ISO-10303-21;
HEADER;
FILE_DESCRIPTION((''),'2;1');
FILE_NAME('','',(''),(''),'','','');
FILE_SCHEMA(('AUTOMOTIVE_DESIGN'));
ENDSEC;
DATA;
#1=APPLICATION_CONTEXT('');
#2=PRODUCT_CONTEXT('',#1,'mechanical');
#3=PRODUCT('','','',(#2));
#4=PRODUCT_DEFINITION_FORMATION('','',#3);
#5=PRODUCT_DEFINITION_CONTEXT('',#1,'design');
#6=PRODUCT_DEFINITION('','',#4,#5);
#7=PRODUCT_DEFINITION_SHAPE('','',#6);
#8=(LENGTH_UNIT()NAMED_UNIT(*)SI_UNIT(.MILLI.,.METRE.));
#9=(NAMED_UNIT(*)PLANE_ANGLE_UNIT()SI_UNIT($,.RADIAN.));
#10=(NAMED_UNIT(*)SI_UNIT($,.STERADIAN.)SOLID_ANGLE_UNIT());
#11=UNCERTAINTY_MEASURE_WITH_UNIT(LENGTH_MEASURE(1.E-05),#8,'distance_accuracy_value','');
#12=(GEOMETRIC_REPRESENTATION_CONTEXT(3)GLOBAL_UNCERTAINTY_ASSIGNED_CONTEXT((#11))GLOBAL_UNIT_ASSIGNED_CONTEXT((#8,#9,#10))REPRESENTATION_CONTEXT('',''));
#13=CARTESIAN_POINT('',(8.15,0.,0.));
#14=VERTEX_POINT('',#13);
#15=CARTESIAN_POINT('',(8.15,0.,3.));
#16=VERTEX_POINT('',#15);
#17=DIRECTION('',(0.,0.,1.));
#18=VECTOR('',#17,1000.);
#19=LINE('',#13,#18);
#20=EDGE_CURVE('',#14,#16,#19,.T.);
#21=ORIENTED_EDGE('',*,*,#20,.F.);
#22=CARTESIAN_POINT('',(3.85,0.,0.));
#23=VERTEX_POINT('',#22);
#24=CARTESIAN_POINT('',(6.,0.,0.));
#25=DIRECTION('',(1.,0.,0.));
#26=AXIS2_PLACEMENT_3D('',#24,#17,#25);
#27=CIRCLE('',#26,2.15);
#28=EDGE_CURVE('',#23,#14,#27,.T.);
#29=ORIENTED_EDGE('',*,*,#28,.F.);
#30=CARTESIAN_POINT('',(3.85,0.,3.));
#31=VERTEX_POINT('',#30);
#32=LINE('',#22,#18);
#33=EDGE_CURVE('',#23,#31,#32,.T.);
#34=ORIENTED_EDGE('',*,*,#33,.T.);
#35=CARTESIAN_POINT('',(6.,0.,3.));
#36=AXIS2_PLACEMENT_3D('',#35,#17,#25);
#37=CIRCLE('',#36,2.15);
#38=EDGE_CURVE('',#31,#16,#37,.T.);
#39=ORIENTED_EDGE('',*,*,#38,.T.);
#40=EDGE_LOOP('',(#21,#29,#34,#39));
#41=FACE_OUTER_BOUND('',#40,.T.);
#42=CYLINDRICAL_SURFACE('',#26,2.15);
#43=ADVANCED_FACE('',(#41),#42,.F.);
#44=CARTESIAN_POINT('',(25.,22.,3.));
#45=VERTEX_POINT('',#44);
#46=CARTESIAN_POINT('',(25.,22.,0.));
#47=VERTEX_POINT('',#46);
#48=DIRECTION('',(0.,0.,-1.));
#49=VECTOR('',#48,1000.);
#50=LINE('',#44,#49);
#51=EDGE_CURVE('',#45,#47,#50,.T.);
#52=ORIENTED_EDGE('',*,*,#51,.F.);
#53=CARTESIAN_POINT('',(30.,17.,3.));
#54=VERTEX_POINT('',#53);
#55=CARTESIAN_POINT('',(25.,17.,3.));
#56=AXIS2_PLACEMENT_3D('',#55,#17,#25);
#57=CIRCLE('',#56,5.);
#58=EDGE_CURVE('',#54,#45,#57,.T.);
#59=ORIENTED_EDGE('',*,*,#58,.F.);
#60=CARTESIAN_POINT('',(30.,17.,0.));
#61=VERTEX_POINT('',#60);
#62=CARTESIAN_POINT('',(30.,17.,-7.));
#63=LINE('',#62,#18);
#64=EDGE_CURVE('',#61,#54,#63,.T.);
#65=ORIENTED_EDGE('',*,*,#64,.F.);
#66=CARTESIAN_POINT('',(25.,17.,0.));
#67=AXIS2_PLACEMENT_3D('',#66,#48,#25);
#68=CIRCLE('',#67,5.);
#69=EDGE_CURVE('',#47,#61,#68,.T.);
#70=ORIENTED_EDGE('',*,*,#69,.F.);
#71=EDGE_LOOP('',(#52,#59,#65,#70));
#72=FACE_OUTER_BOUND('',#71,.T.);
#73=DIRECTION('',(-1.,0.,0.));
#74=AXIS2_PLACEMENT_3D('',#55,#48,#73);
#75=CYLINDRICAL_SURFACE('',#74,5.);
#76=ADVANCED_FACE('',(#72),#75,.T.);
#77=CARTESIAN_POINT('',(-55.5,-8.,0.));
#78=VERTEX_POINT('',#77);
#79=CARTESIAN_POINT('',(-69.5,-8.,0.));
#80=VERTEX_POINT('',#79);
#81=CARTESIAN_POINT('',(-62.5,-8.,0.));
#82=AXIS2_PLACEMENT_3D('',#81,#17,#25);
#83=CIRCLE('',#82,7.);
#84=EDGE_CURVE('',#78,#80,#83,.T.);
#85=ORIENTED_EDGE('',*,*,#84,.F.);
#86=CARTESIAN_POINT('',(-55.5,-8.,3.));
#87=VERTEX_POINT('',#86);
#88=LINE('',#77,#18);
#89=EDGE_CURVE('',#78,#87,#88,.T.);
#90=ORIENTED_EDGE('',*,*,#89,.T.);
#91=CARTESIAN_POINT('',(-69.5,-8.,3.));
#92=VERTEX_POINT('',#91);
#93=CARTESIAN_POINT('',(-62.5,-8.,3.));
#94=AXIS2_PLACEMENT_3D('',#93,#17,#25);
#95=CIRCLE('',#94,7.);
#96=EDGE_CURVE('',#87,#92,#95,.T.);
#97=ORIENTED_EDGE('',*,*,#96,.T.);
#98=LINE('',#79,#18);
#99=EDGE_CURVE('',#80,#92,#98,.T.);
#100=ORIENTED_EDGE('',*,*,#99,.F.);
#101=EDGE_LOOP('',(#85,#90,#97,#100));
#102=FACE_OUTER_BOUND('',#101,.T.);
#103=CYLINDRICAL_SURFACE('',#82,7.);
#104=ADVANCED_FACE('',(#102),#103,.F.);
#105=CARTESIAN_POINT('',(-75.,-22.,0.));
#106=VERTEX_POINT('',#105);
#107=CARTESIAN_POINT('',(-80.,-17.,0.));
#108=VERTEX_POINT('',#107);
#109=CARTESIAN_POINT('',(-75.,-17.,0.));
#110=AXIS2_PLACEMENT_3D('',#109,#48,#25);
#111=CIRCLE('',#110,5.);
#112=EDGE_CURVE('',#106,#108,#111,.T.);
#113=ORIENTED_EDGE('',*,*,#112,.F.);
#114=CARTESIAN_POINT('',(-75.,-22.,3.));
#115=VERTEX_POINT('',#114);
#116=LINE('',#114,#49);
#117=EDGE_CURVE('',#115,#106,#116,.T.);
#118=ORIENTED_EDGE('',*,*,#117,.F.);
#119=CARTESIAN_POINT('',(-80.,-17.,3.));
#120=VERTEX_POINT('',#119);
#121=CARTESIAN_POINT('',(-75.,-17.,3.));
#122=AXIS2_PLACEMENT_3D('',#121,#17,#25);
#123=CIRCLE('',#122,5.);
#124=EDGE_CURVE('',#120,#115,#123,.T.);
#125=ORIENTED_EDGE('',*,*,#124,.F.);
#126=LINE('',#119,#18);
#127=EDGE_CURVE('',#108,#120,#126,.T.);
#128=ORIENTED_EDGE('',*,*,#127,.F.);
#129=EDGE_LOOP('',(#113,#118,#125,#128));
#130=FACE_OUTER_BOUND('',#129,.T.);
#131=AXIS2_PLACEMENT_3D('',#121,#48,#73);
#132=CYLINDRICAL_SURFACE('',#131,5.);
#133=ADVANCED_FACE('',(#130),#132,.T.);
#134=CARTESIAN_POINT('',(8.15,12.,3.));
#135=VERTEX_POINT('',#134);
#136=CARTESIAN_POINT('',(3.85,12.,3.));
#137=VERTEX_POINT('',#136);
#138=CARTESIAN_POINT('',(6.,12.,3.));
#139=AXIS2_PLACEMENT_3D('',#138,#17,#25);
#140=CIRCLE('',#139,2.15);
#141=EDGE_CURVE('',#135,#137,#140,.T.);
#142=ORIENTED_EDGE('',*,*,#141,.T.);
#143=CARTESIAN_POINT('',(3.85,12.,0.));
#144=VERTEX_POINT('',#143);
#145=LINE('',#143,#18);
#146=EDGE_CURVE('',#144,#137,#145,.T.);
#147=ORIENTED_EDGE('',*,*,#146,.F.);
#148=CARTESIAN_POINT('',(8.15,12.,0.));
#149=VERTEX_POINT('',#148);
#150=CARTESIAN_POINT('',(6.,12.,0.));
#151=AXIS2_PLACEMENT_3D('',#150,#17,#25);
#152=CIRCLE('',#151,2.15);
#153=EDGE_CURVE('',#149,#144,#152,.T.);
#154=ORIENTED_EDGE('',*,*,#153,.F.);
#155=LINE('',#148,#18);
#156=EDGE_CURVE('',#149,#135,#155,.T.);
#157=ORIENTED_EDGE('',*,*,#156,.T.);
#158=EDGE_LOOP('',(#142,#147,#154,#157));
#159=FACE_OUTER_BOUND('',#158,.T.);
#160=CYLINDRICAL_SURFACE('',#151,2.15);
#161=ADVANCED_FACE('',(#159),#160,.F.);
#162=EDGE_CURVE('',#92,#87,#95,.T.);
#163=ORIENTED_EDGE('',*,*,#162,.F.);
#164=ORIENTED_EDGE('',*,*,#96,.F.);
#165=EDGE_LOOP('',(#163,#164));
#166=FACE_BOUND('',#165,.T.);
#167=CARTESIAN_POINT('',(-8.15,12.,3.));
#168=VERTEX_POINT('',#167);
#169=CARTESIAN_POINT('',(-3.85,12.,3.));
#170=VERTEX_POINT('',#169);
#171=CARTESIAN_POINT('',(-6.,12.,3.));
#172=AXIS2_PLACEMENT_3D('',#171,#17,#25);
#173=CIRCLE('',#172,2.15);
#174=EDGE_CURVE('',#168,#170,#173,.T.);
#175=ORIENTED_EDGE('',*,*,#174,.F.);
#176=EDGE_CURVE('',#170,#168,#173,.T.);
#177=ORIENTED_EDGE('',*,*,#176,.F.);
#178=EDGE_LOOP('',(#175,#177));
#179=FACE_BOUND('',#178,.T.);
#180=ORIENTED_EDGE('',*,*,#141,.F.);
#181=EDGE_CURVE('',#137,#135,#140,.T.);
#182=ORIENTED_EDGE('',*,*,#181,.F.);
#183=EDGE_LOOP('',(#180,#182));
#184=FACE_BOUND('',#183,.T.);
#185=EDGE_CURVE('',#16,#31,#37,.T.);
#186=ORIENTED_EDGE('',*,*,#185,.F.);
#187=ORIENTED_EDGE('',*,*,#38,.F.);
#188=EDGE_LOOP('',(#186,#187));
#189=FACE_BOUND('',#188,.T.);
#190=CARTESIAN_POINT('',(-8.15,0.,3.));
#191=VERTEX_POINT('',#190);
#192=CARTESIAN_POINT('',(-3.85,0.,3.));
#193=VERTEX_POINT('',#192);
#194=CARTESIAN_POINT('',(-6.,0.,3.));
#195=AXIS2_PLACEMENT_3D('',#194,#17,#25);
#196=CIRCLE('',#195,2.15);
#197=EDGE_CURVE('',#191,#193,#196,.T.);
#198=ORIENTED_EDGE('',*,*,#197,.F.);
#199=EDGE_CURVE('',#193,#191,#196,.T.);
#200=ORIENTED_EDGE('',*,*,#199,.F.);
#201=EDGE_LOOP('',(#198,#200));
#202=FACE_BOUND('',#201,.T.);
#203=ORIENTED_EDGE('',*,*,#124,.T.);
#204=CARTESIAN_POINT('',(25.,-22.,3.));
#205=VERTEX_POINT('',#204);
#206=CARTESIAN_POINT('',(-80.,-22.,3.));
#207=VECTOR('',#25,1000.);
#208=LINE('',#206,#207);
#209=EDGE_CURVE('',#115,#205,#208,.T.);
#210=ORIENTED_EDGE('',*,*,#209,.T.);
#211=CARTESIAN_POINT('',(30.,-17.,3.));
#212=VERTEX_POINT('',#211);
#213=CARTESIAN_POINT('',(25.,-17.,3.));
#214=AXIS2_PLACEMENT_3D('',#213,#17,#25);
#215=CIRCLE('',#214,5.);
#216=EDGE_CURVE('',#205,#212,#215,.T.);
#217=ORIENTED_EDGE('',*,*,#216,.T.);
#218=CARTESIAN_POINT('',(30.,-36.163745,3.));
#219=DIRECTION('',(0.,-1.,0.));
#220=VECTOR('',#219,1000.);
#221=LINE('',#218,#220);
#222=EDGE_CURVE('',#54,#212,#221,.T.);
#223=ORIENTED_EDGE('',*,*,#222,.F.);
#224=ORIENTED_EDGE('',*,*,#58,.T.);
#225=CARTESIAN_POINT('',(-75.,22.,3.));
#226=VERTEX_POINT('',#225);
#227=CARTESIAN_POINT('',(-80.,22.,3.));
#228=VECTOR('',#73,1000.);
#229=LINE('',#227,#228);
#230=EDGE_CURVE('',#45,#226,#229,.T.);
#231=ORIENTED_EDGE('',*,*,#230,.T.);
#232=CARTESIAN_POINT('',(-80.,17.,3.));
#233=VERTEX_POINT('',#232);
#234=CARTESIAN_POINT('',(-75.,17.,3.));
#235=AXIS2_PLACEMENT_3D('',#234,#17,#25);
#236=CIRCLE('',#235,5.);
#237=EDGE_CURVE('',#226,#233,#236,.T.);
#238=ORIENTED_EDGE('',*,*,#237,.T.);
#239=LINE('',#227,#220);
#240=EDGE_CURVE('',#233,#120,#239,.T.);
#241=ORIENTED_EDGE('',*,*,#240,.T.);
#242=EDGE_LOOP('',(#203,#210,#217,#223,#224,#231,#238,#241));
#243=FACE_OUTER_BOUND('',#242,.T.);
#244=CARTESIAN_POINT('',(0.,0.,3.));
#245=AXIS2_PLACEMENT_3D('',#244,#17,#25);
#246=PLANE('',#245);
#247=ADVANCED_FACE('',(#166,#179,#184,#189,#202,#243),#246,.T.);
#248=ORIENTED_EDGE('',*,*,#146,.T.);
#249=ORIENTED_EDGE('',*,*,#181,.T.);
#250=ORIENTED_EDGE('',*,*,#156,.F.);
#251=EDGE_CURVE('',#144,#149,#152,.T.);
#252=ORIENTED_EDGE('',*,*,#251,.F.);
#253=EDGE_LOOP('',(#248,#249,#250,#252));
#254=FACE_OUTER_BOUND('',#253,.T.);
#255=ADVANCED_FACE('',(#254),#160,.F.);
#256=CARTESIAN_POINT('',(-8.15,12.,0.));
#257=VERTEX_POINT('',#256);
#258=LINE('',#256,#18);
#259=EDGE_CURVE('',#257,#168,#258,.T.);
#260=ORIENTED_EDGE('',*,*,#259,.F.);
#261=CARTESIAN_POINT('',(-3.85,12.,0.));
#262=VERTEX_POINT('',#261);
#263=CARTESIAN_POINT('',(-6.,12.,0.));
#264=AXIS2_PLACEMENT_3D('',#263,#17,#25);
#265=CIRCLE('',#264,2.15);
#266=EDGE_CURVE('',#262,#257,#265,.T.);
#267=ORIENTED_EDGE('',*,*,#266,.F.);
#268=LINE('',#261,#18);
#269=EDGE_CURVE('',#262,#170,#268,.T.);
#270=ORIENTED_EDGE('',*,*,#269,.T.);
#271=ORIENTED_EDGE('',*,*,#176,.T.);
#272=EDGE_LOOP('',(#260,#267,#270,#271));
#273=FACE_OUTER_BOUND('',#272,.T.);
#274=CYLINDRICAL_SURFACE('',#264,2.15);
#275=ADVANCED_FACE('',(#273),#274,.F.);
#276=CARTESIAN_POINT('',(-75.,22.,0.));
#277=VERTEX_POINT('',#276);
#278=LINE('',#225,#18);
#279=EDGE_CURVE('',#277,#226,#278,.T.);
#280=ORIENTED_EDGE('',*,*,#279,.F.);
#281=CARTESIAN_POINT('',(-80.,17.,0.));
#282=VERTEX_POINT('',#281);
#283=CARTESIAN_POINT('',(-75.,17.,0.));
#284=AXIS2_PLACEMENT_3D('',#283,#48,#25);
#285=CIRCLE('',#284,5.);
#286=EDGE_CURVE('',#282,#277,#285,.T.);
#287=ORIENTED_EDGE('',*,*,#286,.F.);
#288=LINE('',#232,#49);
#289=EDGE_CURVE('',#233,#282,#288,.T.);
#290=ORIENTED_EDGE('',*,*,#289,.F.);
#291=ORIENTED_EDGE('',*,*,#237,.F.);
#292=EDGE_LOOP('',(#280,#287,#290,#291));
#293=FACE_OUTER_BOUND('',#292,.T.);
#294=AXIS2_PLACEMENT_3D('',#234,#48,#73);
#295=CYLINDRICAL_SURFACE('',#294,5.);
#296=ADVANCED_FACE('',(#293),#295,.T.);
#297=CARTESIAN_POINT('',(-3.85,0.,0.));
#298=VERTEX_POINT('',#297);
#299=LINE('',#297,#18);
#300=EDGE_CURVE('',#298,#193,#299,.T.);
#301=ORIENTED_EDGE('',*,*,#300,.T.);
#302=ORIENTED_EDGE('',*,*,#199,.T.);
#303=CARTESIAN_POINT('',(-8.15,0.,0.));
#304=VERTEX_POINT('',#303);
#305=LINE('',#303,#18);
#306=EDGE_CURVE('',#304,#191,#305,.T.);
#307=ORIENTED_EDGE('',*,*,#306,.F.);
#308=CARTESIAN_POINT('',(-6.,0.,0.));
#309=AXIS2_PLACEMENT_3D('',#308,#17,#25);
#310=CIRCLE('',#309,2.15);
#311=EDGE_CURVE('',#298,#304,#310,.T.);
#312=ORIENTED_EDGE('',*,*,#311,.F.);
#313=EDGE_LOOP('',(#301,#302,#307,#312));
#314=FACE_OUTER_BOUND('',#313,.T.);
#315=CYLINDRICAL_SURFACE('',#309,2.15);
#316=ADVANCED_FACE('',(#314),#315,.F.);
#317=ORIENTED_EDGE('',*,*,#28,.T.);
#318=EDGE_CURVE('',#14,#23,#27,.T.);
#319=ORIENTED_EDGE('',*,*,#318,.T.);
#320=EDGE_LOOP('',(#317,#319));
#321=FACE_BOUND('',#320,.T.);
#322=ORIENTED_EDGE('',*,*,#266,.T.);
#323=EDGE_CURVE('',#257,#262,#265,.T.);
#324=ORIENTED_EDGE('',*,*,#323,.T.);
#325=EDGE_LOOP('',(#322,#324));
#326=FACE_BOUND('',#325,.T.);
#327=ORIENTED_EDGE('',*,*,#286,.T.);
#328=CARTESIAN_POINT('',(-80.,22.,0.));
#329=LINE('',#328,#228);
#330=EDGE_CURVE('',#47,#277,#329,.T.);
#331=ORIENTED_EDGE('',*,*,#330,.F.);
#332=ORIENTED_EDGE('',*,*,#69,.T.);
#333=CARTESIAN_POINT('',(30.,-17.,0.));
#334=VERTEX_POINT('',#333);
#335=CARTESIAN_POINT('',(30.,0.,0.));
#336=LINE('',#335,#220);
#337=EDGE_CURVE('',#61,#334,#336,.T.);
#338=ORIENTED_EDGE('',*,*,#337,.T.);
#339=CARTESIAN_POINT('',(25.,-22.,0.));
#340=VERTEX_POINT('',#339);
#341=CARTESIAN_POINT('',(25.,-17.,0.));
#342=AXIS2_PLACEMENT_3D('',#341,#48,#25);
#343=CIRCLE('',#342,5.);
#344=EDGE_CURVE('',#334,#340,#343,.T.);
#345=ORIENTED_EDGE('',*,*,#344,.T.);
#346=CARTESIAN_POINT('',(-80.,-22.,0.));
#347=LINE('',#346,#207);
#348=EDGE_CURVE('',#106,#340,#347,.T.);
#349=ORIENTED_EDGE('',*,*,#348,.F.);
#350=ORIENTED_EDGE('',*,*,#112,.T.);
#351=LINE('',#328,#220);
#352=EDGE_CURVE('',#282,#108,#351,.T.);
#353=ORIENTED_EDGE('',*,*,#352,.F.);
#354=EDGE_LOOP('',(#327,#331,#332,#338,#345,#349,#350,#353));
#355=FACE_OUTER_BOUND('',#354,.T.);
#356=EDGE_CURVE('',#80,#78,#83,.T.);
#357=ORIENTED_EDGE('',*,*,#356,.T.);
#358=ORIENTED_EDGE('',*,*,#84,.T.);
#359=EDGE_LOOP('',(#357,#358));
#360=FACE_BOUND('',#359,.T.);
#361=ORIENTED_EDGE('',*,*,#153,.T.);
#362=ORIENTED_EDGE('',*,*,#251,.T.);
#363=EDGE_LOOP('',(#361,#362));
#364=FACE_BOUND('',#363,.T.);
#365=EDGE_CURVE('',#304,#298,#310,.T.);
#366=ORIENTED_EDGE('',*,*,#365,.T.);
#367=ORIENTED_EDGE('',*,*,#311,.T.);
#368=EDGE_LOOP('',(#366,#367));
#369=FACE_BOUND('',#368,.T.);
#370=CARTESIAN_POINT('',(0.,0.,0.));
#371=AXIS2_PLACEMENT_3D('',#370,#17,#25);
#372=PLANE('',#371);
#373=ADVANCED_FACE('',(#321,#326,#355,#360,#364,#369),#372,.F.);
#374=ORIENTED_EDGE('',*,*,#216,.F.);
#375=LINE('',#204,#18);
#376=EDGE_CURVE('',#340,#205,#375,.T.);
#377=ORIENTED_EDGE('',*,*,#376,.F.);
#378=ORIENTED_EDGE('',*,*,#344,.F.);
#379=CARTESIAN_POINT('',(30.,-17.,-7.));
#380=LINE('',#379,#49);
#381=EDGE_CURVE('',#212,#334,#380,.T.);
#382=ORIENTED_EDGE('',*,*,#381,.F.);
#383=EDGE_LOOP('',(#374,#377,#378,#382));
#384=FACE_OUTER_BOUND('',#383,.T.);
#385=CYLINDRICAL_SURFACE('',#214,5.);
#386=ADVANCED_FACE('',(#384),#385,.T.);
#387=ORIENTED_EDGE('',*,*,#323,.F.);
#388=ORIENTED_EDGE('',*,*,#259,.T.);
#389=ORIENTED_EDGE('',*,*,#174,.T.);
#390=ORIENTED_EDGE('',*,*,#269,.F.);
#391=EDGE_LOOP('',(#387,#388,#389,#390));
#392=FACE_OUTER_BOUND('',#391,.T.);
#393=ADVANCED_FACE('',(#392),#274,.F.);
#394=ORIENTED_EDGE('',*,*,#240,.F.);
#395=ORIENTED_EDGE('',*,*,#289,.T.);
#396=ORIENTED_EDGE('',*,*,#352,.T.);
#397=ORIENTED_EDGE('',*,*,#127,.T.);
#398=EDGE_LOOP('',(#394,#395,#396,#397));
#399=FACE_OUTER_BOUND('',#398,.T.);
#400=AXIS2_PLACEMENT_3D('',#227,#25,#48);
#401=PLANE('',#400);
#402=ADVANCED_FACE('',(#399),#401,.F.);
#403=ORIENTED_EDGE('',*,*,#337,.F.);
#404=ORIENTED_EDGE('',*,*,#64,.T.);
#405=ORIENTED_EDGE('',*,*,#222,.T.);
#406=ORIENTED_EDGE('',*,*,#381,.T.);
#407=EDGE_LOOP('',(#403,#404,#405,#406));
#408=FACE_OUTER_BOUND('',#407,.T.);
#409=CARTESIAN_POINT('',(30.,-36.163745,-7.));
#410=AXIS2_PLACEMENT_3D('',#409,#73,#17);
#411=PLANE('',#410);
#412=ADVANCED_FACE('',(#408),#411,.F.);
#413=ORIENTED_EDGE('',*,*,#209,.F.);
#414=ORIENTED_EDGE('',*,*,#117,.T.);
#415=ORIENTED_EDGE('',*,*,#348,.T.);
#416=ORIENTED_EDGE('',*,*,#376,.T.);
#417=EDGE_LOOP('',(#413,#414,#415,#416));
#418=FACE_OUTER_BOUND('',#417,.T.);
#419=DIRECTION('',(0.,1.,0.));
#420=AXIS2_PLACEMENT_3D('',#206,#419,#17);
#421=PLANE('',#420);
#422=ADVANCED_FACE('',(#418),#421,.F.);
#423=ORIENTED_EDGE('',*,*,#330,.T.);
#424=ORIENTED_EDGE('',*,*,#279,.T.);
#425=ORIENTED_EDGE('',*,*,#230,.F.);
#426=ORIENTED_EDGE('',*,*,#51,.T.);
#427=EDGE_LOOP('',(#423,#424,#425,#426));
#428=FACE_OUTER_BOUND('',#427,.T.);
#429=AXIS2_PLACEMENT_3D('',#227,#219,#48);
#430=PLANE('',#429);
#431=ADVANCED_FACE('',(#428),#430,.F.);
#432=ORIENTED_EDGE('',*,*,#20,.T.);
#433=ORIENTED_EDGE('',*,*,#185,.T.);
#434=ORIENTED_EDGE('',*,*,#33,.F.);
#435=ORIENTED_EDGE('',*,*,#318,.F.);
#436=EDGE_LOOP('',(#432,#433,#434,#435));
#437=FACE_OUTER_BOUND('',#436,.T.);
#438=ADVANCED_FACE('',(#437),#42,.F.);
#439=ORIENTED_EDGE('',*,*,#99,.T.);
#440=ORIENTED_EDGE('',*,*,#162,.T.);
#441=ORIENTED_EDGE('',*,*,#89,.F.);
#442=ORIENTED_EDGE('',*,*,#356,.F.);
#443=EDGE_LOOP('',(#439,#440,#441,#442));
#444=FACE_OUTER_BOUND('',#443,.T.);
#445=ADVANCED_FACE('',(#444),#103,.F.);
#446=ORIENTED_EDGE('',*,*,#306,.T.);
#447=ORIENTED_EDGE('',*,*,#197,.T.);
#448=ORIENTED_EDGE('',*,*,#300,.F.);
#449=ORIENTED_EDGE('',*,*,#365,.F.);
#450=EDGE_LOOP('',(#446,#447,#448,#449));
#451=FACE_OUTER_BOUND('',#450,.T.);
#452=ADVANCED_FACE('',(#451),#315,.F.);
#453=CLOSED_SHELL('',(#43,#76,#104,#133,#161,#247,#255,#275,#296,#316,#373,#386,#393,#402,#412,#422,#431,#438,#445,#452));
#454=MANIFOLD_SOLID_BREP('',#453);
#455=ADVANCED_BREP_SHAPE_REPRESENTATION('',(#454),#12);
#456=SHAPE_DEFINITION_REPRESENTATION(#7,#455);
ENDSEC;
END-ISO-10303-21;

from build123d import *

# Parameters (mm, degrees)
SKETCH_1_W          = 160
SKETCH_1_H          = 44
EXTRUDE_1_DEPTH     = 3
SKETCH_2_R          = 7
SKETCH_2_R_2        = 2.15
CUT_EXTRUDE_1_DEPTH = 3
FILLET_1_R          = 5
SKETCH_3_W          = 63.678392254
SKETCH_3_H          = 72.512670224
CUT_EXTRUDE_2_DEPTH = 10
FILLET_2_R          = 5


with BuildPart() as part:
    # 草图1 → 凸台-拉伸1 (new body)
    with BuildSketch(Plane.XY):
        Rectangle(SKETCH_1_W, SKETCH_1_H)
    extrude(amount=EXTRUDE_1_DEPTH)

    # 草图2 → 切除-拉伸1 (cut)
    with BuildSketch(Plane.XY.offset(3)):
        with Locations((-62.5, -8)):
            Circle(SKETCH_2_R)
        with Locations((62.5, -8)):
            Circle(SKETCH_2_R)
        with Locations((-6, 12)):
            Circle(SKETCH_2_R_2)
        with Locations((6, 12)):
            Circle(SKETCH_2_R_2)
        with Locations((6, 0)):
            Circle(SKETCH_2_R_2)
        with Locations((-6, 0)):
            Circle(SKETCH_2_R_2)
    extrude(amount=-CUT_EXTRUDE_1_DEPTH, mode=Mode.SUBTRACT)

    # 圆角1
    fillet_1_edges = [part.edges().sort_by_distance(p)[0] for p in [
        (80, -22, 1.5),
        (-80, -22, 1.5),
        (-80, 22, 1.5),
        (80, 22, 1.5),
    ]]
    fillet(fillet_1_edges, radius=FILLET_1_R)

    # 草图3 → 切除-拉伸2 (cut)
    with BuildSketch(Plane.XY.offset(3)):
        with Locations((61.839196127, 0.092590352)):
            Rectangle(SKETCH_3_W, SKETCH_3_H)
    extrude(amount=-CUT_EXTRUDE_2_DEPTH, mode=Mode.SUBTRACT)

    # 圆角2
    fillet_2_edges = [part.edges().sort_by_distance(p)[0] for p in [
        (30, 22, 1.5),
        (30, -22, 1.5),
    ]]
    fillet(fillet_2_edges, radius=FILLET_2_R)


solid = part.part
